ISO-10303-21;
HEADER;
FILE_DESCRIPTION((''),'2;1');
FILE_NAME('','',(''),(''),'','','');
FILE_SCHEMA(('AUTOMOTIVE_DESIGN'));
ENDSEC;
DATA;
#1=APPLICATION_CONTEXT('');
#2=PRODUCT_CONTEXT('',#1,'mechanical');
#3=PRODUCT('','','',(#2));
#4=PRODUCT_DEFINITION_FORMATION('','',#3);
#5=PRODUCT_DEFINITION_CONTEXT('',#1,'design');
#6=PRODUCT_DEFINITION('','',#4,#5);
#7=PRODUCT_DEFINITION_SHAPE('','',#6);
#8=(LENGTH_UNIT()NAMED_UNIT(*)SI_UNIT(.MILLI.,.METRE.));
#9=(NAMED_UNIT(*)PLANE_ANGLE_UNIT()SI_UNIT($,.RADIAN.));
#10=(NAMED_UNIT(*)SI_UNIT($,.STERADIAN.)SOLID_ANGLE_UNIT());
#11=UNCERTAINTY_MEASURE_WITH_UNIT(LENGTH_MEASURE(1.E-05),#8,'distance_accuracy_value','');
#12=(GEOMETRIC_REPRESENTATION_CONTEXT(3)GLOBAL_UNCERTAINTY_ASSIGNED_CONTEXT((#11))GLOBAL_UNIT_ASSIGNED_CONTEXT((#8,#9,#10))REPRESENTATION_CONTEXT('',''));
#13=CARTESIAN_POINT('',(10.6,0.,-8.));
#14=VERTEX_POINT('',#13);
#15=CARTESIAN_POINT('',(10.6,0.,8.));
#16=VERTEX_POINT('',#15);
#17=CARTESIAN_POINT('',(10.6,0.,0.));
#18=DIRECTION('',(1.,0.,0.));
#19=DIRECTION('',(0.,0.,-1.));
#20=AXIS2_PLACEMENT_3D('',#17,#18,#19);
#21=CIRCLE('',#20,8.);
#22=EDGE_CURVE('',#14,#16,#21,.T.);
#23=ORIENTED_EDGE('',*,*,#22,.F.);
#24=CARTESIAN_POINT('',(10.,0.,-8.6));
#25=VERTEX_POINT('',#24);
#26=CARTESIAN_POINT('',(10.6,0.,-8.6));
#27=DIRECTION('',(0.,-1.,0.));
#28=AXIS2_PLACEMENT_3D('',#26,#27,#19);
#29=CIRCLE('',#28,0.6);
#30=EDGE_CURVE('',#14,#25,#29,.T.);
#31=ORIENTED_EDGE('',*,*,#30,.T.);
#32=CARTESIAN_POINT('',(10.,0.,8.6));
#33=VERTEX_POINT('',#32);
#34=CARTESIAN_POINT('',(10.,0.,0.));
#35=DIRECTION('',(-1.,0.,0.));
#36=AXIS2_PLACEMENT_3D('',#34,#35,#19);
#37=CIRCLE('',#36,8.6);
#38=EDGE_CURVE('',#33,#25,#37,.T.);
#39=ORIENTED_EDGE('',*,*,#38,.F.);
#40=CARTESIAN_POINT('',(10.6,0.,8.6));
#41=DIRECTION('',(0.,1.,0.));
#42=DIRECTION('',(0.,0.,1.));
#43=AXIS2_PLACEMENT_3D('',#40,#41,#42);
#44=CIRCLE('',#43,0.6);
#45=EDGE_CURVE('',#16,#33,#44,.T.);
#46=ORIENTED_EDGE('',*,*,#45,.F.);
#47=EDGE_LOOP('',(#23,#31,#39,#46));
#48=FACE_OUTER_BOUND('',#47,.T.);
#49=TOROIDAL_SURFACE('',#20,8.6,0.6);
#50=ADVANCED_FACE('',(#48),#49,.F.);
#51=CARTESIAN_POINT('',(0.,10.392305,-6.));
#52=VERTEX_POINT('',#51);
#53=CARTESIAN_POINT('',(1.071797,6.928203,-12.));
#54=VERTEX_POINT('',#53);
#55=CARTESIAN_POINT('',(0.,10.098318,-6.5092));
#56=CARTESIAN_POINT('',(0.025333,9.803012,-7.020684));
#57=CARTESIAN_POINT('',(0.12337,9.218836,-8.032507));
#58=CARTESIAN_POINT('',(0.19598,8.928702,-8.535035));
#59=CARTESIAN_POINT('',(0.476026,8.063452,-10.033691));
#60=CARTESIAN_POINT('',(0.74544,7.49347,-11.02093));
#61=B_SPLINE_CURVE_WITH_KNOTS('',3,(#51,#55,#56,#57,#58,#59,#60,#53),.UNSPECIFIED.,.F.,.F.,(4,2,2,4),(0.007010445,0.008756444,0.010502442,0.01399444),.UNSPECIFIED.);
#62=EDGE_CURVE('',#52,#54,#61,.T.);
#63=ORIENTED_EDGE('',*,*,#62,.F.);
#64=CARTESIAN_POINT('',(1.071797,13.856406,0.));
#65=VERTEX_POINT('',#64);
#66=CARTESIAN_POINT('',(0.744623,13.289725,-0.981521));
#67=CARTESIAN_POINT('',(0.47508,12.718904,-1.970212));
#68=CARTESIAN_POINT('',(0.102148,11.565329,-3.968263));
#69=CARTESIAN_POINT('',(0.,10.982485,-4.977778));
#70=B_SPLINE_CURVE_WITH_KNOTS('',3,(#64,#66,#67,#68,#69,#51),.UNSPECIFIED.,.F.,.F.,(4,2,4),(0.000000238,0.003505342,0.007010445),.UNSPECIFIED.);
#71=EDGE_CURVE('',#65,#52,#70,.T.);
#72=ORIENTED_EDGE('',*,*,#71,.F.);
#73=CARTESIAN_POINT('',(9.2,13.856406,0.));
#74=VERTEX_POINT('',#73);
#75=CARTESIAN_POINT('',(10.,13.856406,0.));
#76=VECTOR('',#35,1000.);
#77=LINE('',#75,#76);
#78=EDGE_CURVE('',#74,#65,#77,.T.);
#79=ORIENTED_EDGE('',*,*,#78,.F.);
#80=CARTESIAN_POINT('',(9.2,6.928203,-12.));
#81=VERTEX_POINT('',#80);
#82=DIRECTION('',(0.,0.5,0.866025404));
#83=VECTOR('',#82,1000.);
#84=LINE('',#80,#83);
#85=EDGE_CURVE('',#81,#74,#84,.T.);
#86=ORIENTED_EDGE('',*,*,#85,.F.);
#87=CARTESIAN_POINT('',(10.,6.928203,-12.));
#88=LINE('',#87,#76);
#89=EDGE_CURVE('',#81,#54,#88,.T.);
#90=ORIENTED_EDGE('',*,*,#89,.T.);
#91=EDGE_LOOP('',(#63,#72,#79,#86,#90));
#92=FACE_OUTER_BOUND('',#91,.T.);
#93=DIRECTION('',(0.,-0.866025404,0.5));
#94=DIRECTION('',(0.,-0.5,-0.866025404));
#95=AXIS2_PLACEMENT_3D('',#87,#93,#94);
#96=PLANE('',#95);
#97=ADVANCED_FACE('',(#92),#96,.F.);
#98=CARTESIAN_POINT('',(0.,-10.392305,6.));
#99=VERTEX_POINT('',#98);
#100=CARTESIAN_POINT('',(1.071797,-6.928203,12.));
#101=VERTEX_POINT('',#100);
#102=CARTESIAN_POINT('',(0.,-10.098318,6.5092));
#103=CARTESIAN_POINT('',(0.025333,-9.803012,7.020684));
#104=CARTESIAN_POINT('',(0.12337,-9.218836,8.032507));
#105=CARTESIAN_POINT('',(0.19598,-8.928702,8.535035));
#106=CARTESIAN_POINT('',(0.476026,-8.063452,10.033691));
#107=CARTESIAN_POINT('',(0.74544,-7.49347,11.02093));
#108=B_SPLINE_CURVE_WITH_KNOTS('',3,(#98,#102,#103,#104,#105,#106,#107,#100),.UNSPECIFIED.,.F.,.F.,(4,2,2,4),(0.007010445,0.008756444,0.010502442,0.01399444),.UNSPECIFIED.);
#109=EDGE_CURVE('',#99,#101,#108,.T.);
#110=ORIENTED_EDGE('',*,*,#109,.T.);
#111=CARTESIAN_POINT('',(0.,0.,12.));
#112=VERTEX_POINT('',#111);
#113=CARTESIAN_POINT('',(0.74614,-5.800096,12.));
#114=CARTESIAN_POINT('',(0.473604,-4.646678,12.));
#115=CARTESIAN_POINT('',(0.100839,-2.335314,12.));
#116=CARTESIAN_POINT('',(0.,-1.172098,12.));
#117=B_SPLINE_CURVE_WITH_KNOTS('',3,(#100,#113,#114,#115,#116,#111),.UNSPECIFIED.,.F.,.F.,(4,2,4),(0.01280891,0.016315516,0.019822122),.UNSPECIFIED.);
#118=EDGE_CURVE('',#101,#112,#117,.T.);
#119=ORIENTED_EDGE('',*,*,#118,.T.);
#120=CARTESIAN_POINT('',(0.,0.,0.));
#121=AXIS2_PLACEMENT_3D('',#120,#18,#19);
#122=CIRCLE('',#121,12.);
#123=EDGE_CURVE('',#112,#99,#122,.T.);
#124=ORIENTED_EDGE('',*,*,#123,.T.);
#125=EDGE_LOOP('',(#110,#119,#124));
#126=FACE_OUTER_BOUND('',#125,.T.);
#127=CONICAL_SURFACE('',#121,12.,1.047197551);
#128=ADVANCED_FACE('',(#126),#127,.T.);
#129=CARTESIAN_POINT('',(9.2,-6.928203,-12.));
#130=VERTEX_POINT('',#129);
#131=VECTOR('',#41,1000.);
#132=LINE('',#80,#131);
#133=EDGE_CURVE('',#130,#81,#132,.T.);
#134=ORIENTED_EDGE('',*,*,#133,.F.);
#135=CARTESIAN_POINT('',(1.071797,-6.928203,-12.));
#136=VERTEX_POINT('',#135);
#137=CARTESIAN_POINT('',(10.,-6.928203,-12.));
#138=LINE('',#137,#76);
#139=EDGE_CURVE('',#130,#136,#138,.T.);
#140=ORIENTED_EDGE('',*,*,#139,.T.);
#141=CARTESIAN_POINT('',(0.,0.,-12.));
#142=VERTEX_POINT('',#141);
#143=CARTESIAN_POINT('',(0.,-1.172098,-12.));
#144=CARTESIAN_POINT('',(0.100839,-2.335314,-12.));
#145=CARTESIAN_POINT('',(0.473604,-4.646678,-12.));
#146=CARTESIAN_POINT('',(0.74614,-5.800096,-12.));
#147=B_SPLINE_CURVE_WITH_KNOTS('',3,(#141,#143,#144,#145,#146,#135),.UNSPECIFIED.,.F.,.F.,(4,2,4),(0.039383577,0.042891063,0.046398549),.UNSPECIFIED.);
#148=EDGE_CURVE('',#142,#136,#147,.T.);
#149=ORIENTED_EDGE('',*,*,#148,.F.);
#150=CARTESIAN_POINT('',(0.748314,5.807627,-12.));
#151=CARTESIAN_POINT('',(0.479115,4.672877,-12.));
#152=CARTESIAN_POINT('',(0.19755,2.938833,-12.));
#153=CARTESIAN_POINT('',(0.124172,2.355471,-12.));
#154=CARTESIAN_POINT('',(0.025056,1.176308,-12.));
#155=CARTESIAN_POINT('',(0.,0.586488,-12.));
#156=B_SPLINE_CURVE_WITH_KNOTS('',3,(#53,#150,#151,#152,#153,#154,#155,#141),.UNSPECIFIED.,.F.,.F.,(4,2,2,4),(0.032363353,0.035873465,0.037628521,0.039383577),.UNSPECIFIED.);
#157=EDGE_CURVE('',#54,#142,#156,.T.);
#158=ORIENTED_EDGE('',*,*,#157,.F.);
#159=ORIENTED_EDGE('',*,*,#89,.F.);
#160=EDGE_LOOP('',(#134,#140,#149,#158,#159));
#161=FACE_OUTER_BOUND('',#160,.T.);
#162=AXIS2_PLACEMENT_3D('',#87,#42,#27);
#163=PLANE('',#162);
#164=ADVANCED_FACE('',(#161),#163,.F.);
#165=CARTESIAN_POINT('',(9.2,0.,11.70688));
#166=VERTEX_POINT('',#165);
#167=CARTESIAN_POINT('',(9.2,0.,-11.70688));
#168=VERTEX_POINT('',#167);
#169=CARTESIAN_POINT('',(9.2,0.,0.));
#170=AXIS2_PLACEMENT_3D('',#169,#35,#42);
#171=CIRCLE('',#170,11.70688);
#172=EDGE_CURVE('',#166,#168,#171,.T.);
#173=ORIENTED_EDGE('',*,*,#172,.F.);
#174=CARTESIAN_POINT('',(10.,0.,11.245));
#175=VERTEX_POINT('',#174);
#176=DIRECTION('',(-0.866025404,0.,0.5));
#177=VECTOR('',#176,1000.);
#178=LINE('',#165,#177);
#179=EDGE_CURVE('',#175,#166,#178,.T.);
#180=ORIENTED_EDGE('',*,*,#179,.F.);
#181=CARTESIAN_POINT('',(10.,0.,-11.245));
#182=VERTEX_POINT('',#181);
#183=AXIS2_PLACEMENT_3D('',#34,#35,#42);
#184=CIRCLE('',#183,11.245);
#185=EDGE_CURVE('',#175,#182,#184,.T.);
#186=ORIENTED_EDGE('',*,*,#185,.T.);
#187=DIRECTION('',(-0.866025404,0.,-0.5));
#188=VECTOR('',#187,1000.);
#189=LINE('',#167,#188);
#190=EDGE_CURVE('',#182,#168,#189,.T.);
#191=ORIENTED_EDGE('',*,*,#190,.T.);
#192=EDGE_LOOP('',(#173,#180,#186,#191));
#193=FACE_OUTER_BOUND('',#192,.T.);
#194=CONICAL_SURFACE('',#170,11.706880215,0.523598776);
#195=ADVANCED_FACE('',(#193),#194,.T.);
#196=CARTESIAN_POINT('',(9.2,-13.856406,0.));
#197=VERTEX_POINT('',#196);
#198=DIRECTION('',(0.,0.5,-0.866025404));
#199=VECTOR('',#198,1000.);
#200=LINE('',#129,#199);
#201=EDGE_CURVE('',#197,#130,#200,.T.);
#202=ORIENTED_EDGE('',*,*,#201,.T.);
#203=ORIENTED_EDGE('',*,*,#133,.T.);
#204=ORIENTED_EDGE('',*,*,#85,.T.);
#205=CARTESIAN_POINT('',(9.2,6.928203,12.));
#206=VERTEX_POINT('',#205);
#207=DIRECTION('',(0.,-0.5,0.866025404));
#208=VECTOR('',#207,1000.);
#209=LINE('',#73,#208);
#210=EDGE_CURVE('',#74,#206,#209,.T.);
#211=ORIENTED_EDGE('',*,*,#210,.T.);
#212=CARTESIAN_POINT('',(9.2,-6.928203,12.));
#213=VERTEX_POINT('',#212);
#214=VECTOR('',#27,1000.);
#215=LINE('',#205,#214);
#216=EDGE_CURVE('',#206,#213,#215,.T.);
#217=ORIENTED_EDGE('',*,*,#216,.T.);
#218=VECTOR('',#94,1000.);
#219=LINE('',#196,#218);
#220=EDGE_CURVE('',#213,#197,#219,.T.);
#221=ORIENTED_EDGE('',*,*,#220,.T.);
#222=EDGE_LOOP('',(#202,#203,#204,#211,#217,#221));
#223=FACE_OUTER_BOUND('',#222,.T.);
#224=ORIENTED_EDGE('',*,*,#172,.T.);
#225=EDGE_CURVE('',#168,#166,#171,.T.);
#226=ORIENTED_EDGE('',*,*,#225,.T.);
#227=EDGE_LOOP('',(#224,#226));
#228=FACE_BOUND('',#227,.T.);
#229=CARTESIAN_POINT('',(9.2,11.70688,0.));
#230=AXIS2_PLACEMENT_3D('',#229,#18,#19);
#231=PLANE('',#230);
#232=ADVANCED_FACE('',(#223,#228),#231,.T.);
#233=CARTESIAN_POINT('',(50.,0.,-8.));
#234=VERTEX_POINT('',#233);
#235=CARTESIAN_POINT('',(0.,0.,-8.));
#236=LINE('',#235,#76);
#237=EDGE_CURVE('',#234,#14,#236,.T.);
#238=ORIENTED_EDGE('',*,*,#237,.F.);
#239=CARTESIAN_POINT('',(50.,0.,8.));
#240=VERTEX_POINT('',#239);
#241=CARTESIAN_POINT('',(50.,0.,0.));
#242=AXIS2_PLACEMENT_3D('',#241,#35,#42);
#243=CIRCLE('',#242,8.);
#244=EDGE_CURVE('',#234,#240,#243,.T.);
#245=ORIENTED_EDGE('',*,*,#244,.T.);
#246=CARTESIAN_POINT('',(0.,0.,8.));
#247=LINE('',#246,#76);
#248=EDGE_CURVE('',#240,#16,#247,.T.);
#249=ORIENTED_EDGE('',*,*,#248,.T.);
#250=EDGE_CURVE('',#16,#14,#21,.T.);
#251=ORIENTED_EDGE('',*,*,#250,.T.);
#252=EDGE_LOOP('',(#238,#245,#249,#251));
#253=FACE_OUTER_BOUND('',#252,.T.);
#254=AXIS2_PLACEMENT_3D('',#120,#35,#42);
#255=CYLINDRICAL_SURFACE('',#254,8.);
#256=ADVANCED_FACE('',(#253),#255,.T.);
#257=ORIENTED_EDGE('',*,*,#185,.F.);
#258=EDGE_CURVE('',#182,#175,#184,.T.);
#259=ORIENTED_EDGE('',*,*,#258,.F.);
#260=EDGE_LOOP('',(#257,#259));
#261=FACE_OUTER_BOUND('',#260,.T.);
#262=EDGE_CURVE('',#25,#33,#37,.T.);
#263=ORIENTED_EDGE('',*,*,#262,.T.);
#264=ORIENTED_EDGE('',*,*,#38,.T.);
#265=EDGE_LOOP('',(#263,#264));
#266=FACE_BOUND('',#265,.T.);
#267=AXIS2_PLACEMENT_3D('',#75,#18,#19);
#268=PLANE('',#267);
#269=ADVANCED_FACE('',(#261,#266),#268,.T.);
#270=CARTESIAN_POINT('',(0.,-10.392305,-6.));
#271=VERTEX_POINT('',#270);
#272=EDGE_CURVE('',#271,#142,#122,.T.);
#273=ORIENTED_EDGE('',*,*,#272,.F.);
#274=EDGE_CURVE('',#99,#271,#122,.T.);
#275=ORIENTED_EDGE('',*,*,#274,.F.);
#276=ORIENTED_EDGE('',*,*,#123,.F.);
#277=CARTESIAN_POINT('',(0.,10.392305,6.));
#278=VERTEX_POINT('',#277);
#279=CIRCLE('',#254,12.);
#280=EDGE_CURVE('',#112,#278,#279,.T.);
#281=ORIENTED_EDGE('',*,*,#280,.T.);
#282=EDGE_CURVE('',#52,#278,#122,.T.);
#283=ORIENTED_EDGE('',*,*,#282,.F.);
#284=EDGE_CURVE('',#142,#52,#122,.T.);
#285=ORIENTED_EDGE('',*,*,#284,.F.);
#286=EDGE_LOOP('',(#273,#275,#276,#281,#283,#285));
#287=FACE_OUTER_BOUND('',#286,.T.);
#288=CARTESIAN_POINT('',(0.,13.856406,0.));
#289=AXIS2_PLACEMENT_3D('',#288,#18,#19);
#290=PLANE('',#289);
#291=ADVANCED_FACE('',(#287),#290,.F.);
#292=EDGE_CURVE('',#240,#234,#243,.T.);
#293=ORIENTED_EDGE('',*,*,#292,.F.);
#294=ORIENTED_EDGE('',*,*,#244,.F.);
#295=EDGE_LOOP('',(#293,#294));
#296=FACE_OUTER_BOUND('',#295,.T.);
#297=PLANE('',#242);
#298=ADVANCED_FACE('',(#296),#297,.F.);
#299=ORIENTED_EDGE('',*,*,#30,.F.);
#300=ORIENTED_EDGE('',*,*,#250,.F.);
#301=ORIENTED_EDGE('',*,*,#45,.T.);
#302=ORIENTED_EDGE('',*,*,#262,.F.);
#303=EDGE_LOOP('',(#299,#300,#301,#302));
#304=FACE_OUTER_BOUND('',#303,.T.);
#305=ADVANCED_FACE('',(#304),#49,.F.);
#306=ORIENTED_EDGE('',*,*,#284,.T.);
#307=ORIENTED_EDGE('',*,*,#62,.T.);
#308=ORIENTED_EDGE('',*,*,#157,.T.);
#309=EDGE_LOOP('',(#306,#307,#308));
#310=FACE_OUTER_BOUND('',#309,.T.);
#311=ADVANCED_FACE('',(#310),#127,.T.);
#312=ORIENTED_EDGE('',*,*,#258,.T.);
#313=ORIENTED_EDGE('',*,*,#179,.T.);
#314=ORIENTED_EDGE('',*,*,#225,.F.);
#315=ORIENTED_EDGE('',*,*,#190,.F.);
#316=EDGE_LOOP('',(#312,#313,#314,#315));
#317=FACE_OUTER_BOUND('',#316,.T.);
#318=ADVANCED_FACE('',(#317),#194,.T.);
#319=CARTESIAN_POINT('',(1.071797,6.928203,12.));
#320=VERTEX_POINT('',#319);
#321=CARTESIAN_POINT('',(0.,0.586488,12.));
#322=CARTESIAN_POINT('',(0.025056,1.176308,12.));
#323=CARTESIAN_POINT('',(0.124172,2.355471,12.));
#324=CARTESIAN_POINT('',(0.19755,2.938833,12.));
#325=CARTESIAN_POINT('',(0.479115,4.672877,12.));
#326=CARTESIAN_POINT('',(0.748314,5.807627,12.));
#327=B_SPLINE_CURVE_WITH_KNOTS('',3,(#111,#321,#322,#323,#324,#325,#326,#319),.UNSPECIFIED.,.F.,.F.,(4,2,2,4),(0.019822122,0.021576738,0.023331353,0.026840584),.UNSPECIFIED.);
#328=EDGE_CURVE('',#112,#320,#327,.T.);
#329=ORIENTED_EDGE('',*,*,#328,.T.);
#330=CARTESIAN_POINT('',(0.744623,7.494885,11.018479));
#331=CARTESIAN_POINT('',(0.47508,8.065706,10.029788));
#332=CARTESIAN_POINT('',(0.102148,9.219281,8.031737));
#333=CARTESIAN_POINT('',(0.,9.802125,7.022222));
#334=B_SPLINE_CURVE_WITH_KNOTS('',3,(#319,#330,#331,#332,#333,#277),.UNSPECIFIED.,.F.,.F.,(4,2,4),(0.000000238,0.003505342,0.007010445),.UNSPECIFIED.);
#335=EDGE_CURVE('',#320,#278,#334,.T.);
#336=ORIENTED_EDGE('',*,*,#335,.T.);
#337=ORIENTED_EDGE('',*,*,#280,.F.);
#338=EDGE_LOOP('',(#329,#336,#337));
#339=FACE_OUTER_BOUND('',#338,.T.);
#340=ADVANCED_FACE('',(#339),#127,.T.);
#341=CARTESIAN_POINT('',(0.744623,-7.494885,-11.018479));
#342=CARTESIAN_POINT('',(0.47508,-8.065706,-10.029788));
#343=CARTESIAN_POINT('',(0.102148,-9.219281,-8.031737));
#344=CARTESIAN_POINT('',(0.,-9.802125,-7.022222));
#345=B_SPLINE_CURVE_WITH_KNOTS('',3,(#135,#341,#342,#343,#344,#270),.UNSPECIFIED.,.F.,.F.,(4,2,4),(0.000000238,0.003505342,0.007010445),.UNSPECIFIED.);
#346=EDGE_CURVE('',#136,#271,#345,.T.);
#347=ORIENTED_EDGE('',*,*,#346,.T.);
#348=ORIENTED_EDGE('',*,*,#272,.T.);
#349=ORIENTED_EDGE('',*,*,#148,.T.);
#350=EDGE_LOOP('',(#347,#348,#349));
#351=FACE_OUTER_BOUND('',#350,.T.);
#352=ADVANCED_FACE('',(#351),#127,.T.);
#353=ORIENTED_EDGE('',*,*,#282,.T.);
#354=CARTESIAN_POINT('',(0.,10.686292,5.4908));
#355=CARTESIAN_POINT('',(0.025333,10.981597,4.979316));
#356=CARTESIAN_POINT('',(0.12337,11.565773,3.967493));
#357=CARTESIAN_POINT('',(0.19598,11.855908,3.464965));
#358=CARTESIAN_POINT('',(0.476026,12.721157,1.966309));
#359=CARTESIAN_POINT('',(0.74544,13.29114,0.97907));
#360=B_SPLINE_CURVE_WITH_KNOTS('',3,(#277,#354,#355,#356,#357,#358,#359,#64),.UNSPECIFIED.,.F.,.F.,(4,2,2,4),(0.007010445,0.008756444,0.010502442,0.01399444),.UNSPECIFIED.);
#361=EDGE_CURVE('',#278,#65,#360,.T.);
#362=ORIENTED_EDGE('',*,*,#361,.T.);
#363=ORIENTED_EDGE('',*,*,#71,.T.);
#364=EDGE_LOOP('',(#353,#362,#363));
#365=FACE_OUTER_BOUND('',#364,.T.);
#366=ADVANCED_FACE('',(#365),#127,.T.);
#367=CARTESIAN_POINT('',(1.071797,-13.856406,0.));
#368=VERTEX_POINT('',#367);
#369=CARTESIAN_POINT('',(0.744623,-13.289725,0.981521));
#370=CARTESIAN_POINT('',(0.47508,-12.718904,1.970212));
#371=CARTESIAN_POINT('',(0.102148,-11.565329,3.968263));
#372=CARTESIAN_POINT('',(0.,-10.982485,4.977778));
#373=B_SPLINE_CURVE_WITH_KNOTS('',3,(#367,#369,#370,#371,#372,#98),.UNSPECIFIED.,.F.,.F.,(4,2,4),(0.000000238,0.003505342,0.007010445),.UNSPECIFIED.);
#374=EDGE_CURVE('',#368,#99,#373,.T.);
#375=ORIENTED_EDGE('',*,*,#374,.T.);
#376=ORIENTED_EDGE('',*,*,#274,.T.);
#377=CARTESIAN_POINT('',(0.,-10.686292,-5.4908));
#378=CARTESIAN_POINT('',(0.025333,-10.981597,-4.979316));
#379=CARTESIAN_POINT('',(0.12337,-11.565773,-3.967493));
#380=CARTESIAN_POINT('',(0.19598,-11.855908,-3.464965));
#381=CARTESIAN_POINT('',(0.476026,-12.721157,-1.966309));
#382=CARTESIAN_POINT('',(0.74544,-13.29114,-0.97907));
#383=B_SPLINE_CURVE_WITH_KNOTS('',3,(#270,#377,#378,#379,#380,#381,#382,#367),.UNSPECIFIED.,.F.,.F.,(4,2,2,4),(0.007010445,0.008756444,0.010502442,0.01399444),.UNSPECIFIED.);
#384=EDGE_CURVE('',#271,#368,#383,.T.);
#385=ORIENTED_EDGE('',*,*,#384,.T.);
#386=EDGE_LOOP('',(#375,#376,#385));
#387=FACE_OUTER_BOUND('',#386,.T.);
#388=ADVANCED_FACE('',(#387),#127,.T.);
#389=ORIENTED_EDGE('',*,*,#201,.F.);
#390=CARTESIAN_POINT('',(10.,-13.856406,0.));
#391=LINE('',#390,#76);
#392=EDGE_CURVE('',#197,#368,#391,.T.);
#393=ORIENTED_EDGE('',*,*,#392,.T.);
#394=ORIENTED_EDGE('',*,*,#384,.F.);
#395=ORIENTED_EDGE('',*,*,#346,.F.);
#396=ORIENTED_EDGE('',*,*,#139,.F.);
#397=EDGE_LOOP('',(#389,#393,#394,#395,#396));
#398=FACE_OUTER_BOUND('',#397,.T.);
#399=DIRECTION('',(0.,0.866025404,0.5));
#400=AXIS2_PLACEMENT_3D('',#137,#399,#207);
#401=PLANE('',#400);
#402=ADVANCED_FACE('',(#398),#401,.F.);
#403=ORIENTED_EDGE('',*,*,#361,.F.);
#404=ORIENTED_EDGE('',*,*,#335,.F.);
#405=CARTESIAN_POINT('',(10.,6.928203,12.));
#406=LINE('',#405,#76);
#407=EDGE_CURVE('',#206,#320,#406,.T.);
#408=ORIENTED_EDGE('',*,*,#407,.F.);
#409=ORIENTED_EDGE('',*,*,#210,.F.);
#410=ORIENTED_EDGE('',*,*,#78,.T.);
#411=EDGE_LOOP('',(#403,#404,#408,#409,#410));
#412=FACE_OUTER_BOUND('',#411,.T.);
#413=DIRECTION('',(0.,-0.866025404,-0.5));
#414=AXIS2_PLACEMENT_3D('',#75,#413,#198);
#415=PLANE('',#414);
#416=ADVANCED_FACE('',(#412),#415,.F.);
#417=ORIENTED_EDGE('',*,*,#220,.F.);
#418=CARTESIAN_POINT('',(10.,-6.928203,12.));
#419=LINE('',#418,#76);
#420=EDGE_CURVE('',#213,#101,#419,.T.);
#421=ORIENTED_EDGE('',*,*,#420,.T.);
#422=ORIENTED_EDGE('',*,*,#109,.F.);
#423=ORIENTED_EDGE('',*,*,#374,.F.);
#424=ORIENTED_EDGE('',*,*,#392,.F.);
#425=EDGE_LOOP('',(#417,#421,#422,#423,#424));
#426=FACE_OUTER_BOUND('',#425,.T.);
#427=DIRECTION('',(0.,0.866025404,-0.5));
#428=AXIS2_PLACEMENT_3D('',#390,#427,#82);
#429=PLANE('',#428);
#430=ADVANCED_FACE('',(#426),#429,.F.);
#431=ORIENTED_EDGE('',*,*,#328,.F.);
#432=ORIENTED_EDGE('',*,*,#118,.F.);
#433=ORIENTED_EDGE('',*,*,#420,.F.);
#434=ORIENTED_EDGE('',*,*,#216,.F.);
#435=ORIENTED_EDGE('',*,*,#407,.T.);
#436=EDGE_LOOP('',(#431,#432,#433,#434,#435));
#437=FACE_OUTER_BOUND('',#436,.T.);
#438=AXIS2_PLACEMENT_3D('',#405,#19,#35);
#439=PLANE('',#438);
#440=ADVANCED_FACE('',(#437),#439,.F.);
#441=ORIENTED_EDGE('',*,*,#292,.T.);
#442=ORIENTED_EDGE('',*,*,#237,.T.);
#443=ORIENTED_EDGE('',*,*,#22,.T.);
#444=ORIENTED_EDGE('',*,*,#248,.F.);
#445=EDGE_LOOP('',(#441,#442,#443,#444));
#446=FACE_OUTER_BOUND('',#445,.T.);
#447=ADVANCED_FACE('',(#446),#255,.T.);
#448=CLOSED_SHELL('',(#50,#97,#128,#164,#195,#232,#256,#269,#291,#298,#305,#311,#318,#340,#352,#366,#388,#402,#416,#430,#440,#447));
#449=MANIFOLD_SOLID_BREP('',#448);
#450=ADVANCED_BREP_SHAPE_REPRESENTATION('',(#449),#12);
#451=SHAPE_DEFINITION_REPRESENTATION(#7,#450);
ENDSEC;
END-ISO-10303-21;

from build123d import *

# Parameters (mm, degrees)
EXTRUDE_387_DEPTH = 10
FILLET_1280_R     = 0.6


with BuildPart() as part:
    # 草图1 → Extrude 387 (new body)
    with BuildSketch(Plane(origin=(0, 0, 0), x_dir=(0, 0, -1), z_dir=(1, 0, 0))):
        Polygon((12, 6.92820323), (12, -6.92820323), (0, -13.856406461), (-12, -6.92820323), (-12, 6.92820323), (0, 13.856406461), align=None)
    extrude(amount=EXTRUDE_387_DEPTH)

    # 草图2 → 凸台-旋转1 (revolve)
    with BuildSketch(Plane.XY, mode=Mode.PRIVATE) as revolve_1_sk:
        Polygon((0, 0), (50, 0), (50, 6.268), (50, 8), (12, 8), (0, 8), align=None)
    revolve(revolve_1_sk.sketch.rotate(Axis((0, 0, 0), (1, 0, 0)), 90), axis=Axis((0, 0, 0), (1, 0, 0)))

    # 草图3 → 切除-旋转1 (revolve, cut)
    with BuildSketch(Plane.XY):
        Polygon((0, 12), (3.958548116, 18.856406461), (3.958548116, 23.856406461), (-10, 23.856406461), (-10, 12), align=None)
    revolve(axis=Axis((0, 0, 0), (1, 0, 0)), mode=Mode.SUBTRACT)

    # 草图4 → 切除-旋转3 (revolve, cut)
    with BuildSketch(Plane.XY, mode=Mode.PRIVATE) as cut_revolve_3_sk:
        Polygon((10, 11.245), (9.2, 11.706880215), (9.2, 13.856406461), (10, 13.856406461), align=None)
    revolve(cut_revolve_3_sk.sketch.rotate(Axis((0, 0, 0), (1, 0, 0)), 90), axis=Axis((0, 0, 0), (1, 0, 0)), mode=Mode.SUBTRACT)

    # Fillet 1280
    fillet_1280_edges = [part.edges().sort_by_distance(p)[0] for p in [
        (10, 0, -8),
    ]]
    fillet(fillet_1280_edges, radius=FILLET_1280_R)


solid = part.part
